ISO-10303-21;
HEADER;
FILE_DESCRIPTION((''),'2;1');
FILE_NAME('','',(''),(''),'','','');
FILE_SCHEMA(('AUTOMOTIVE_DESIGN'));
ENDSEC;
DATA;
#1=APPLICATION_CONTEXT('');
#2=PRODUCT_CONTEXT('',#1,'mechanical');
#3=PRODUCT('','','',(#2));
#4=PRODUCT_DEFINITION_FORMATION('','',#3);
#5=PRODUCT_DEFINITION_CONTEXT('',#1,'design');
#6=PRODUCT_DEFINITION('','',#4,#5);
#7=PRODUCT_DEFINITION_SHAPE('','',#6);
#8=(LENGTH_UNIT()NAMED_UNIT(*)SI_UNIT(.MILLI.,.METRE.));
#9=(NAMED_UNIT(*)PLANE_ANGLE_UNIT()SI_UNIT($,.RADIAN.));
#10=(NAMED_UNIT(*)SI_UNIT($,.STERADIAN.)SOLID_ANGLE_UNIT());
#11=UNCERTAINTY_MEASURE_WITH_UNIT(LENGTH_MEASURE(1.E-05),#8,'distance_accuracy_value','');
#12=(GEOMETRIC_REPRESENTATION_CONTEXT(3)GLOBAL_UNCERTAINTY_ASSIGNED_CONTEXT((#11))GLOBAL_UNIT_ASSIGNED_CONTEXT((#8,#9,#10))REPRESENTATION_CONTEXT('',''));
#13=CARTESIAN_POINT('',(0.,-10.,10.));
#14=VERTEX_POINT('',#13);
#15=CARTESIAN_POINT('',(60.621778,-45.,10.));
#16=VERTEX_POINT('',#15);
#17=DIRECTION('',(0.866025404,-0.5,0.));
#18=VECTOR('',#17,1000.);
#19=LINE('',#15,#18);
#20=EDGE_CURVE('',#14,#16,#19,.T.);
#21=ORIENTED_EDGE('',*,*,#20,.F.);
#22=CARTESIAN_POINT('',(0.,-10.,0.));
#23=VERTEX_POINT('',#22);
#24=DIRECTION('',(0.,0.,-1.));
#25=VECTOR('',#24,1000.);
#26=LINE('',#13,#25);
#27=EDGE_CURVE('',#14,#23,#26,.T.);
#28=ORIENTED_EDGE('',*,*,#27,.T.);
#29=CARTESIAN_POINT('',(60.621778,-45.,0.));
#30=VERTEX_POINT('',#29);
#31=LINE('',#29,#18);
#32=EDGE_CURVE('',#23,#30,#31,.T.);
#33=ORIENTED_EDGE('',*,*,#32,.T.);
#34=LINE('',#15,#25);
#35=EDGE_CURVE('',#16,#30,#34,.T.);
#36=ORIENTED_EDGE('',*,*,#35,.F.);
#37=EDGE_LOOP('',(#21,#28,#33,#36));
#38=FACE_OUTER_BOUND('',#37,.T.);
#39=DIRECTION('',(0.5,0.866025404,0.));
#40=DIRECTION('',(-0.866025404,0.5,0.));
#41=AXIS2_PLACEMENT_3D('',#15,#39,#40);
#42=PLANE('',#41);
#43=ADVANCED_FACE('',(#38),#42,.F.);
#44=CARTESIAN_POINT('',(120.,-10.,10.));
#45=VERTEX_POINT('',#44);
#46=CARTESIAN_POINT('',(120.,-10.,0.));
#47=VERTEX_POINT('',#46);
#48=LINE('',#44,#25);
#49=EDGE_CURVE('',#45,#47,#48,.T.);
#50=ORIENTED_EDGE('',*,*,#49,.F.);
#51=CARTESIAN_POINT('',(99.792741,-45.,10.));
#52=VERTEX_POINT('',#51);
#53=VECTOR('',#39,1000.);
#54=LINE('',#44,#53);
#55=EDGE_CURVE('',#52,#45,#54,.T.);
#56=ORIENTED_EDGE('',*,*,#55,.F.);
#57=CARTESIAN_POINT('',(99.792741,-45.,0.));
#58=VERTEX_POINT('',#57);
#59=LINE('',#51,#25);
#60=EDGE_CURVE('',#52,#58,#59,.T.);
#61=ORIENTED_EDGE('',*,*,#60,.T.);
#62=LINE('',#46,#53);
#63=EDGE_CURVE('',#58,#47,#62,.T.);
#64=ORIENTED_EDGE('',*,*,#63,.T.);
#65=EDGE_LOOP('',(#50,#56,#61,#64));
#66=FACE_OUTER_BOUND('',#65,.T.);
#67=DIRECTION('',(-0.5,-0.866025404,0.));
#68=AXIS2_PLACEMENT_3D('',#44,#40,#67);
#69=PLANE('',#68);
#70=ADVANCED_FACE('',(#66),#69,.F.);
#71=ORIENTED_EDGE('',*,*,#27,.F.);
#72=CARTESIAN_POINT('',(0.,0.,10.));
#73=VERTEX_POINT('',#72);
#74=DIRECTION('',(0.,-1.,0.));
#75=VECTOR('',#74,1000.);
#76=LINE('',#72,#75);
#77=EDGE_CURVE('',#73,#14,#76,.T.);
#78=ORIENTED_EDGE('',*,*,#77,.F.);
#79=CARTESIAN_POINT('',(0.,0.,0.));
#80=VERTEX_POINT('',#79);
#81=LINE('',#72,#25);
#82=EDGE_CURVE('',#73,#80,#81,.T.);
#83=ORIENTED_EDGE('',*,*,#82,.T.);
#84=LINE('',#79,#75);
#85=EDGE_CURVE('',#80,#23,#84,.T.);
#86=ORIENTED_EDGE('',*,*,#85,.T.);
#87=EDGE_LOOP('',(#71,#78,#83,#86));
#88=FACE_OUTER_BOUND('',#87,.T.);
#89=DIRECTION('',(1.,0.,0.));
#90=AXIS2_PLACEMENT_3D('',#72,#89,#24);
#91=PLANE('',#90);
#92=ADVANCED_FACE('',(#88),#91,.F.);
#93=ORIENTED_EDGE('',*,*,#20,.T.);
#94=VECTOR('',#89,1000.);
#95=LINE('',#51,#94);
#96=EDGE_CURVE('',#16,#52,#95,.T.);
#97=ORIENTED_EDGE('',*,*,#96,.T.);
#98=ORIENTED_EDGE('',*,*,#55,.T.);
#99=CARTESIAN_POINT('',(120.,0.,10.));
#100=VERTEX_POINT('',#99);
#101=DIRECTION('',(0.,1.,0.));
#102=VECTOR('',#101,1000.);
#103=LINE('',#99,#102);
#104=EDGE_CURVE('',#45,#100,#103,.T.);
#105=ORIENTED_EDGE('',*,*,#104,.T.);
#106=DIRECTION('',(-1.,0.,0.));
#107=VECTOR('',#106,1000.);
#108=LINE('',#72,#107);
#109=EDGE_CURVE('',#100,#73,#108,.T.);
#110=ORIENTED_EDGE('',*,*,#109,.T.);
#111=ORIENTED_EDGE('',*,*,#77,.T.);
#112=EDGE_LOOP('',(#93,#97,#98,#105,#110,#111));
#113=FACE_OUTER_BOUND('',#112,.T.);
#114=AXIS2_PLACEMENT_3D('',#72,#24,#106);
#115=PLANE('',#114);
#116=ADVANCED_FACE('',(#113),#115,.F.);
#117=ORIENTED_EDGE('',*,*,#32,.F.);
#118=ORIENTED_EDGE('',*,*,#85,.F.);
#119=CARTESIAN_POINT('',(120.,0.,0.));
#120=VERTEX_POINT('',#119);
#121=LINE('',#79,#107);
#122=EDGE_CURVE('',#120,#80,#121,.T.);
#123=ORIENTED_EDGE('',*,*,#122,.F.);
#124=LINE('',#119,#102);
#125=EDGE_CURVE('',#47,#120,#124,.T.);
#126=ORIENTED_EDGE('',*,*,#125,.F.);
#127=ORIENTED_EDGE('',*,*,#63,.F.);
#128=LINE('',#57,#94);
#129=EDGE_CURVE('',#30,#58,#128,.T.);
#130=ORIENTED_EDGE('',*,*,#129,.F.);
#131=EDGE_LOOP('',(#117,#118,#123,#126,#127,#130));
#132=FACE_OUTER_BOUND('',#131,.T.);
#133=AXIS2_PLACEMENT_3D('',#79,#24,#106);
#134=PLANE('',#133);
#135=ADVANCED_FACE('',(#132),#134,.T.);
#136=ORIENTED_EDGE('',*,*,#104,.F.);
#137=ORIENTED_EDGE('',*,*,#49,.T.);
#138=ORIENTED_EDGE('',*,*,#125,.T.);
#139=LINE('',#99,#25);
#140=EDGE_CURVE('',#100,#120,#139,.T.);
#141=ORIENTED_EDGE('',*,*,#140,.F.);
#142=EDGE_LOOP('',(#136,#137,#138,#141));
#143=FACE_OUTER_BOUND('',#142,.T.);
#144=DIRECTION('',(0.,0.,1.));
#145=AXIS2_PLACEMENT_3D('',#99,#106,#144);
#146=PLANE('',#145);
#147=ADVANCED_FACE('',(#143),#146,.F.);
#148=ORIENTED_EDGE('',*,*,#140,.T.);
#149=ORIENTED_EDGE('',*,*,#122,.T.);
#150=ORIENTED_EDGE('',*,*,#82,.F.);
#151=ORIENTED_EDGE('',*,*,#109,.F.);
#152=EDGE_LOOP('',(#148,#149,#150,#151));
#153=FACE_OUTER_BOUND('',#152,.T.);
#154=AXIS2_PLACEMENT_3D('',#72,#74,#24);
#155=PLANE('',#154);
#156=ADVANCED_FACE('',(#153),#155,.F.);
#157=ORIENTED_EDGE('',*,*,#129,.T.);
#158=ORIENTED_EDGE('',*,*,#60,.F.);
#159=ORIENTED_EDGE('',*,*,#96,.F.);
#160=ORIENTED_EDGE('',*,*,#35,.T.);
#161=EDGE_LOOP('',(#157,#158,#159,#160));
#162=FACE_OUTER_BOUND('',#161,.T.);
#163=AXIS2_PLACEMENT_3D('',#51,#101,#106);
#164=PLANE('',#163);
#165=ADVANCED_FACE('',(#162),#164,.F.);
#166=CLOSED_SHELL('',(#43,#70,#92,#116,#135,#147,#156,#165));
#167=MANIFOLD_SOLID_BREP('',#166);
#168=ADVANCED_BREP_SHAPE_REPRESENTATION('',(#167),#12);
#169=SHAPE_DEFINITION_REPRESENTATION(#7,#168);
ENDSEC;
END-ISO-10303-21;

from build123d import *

# Parameters (mm, degrees)
BOSS_EXTRUDE1_DEPTH = 10


with BuildPart() as part:
    # Sketch1 → Boss-Extrude1 (new body)
    with BuildSketch(Plane.XY):
        Polygon((0, 0), (120, 0), (120, -10), (99.792740578, -45), (60.621778265, -45), (0, -10), align=None)
    extrude(amount=BOSS_EXTRUDE1_DEPTH)


solid = part.part
